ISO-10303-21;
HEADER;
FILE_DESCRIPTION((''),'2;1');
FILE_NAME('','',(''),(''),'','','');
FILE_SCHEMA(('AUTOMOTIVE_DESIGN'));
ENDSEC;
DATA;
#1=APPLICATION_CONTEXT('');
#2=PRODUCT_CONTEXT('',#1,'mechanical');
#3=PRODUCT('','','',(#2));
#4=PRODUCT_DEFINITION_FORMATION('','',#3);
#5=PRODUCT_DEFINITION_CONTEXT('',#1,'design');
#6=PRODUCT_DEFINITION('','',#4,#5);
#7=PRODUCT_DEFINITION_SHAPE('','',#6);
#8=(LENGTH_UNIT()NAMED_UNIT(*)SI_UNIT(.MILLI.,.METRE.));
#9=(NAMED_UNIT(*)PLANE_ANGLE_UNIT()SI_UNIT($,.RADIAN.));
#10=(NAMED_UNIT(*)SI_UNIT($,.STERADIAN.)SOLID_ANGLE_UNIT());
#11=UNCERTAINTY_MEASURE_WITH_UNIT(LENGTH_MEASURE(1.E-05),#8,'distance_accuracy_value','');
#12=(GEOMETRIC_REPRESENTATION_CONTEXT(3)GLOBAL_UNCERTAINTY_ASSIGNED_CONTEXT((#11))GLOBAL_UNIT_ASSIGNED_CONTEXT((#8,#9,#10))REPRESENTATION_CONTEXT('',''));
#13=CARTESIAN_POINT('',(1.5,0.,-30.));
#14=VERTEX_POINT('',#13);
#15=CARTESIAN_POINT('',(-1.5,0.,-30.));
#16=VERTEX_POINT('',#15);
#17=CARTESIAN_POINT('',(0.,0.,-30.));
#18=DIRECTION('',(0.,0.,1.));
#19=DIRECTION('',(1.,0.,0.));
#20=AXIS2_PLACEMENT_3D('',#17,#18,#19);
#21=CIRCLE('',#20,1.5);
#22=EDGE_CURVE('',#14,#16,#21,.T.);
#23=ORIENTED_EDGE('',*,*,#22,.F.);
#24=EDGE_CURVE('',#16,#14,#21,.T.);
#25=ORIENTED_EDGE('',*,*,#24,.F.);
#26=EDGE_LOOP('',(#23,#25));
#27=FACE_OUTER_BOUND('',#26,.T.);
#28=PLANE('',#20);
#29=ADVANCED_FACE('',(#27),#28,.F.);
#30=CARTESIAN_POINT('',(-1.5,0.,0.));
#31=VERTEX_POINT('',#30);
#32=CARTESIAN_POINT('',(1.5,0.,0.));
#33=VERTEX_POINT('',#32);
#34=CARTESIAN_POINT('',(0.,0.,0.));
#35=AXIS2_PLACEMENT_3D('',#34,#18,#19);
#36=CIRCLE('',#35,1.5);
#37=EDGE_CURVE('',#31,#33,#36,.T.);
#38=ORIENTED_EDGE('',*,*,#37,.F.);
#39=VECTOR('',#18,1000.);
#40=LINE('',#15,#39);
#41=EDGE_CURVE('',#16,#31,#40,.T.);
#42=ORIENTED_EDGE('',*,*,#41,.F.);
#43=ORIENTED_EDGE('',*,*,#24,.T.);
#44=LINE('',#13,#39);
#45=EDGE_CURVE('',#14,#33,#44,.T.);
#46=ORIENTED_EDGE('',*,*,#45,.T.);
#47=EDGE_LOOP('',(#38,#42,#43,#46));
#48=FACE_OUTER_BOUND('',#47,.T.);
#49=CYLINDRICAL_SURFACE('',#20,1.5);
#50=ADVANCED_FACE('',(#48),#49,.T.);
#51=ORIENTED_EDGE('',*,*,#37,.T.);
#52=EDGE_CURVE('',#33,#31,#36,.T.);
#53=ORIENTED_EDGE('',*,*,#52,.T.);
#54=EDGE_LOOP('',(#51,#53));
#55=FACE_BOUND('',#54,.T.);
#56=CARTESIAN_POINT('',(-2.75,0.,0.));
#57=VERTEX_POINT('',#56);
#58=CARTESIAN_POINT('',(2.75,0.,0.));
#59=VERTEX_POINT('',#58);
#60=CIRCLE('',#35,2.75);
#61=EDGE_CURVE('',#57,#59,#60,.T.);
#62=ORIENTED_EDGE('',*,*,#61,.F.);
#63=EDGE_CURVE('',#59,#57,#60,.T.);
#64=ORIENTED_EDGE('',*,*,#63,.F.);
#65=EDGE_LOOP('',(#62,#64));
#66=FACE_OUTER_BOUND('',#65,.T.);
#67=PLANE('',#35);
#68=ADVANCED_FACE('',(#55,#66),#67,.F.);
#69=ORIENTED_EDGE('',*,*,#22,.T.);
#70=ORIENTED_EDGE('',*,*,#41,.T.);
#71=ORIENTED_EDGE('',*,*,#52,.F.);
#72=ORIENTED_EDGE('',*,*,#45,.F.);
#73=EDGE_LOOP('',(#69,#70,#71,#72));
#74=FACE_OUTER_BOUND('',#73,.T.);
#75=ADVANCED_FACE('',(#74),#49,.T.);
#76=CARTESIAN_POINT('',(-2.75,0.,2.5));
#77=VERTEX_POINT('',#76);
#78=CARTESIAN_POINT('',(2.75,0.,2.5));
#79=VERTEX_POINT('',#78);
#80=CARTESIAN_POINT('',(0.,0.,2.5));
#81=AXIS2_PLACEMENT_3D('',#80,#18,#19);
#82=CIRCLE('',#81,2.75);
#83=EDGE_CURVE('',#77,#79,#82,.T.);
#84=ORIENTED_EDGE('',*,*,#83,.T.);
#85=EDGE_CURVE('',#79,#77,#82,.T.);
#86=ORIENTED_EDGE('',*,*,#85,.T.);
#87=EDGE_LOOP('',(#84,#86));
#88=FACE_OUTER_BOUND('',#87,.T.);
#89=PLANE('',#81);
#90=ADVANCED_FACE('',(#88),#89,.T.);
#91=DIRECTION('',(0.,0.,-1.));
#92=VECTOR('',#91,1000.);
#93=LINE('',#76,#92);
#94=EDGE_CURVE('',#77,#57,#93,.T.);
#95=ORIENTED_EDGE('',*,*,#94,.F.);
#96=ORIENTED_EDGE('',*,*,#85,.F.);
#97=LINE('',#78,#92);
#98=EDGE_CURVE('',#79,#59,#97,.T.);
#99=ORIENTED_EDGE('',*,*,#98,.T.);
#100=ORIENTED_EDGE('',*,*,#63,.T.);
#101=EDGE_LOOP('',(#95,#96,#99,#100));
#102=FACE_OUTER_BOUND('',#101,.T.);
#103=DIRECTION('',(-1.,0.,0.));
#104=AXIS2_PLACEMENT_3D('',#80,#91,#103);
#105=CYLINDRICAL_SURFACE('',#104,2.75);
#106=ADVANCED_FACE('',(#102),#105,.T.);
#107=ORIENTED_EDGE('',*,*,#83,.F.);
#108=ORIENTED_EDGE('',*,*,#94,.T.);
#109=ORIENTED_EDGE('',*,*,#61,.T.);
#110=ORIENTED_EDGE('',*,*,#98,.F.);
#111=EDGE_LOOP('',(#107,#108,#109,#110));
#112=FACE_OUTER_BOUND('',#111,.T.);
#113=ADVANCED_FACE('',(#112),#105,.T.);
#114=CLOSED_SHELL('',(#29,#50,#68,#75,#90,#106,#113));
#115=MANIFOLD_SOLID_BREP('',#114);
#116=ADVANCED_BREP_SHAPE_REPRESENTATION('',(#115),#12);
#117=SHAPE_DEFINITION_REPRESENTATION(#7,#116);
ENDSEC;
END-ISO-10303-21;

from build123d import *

# Parameters (mm, degrees)
SKETCH_1_R      = 1.5
EXTRUDE_1_DEPTH = 30
SKETCH_2_R      = 2.75
EXTRUDE_2_DEPTH = 2.5


with BuildPart() as part:
    # 草图1 → 凸台-拉伸1 (new body)
    with BuildSketch(Plane.XY):
        Circle(SKETCH_1_R)
    extrude(amount=-EXTRUDE_1_DEPTH)

    # 草图2 → 凸台-拉伸2 (add)
    with BuildSketch(Plane.XY):
        Circle(SKETCH_2_R)
    extrude(amount=EXTRUDE_2_DEPTH)


solid = part.part
